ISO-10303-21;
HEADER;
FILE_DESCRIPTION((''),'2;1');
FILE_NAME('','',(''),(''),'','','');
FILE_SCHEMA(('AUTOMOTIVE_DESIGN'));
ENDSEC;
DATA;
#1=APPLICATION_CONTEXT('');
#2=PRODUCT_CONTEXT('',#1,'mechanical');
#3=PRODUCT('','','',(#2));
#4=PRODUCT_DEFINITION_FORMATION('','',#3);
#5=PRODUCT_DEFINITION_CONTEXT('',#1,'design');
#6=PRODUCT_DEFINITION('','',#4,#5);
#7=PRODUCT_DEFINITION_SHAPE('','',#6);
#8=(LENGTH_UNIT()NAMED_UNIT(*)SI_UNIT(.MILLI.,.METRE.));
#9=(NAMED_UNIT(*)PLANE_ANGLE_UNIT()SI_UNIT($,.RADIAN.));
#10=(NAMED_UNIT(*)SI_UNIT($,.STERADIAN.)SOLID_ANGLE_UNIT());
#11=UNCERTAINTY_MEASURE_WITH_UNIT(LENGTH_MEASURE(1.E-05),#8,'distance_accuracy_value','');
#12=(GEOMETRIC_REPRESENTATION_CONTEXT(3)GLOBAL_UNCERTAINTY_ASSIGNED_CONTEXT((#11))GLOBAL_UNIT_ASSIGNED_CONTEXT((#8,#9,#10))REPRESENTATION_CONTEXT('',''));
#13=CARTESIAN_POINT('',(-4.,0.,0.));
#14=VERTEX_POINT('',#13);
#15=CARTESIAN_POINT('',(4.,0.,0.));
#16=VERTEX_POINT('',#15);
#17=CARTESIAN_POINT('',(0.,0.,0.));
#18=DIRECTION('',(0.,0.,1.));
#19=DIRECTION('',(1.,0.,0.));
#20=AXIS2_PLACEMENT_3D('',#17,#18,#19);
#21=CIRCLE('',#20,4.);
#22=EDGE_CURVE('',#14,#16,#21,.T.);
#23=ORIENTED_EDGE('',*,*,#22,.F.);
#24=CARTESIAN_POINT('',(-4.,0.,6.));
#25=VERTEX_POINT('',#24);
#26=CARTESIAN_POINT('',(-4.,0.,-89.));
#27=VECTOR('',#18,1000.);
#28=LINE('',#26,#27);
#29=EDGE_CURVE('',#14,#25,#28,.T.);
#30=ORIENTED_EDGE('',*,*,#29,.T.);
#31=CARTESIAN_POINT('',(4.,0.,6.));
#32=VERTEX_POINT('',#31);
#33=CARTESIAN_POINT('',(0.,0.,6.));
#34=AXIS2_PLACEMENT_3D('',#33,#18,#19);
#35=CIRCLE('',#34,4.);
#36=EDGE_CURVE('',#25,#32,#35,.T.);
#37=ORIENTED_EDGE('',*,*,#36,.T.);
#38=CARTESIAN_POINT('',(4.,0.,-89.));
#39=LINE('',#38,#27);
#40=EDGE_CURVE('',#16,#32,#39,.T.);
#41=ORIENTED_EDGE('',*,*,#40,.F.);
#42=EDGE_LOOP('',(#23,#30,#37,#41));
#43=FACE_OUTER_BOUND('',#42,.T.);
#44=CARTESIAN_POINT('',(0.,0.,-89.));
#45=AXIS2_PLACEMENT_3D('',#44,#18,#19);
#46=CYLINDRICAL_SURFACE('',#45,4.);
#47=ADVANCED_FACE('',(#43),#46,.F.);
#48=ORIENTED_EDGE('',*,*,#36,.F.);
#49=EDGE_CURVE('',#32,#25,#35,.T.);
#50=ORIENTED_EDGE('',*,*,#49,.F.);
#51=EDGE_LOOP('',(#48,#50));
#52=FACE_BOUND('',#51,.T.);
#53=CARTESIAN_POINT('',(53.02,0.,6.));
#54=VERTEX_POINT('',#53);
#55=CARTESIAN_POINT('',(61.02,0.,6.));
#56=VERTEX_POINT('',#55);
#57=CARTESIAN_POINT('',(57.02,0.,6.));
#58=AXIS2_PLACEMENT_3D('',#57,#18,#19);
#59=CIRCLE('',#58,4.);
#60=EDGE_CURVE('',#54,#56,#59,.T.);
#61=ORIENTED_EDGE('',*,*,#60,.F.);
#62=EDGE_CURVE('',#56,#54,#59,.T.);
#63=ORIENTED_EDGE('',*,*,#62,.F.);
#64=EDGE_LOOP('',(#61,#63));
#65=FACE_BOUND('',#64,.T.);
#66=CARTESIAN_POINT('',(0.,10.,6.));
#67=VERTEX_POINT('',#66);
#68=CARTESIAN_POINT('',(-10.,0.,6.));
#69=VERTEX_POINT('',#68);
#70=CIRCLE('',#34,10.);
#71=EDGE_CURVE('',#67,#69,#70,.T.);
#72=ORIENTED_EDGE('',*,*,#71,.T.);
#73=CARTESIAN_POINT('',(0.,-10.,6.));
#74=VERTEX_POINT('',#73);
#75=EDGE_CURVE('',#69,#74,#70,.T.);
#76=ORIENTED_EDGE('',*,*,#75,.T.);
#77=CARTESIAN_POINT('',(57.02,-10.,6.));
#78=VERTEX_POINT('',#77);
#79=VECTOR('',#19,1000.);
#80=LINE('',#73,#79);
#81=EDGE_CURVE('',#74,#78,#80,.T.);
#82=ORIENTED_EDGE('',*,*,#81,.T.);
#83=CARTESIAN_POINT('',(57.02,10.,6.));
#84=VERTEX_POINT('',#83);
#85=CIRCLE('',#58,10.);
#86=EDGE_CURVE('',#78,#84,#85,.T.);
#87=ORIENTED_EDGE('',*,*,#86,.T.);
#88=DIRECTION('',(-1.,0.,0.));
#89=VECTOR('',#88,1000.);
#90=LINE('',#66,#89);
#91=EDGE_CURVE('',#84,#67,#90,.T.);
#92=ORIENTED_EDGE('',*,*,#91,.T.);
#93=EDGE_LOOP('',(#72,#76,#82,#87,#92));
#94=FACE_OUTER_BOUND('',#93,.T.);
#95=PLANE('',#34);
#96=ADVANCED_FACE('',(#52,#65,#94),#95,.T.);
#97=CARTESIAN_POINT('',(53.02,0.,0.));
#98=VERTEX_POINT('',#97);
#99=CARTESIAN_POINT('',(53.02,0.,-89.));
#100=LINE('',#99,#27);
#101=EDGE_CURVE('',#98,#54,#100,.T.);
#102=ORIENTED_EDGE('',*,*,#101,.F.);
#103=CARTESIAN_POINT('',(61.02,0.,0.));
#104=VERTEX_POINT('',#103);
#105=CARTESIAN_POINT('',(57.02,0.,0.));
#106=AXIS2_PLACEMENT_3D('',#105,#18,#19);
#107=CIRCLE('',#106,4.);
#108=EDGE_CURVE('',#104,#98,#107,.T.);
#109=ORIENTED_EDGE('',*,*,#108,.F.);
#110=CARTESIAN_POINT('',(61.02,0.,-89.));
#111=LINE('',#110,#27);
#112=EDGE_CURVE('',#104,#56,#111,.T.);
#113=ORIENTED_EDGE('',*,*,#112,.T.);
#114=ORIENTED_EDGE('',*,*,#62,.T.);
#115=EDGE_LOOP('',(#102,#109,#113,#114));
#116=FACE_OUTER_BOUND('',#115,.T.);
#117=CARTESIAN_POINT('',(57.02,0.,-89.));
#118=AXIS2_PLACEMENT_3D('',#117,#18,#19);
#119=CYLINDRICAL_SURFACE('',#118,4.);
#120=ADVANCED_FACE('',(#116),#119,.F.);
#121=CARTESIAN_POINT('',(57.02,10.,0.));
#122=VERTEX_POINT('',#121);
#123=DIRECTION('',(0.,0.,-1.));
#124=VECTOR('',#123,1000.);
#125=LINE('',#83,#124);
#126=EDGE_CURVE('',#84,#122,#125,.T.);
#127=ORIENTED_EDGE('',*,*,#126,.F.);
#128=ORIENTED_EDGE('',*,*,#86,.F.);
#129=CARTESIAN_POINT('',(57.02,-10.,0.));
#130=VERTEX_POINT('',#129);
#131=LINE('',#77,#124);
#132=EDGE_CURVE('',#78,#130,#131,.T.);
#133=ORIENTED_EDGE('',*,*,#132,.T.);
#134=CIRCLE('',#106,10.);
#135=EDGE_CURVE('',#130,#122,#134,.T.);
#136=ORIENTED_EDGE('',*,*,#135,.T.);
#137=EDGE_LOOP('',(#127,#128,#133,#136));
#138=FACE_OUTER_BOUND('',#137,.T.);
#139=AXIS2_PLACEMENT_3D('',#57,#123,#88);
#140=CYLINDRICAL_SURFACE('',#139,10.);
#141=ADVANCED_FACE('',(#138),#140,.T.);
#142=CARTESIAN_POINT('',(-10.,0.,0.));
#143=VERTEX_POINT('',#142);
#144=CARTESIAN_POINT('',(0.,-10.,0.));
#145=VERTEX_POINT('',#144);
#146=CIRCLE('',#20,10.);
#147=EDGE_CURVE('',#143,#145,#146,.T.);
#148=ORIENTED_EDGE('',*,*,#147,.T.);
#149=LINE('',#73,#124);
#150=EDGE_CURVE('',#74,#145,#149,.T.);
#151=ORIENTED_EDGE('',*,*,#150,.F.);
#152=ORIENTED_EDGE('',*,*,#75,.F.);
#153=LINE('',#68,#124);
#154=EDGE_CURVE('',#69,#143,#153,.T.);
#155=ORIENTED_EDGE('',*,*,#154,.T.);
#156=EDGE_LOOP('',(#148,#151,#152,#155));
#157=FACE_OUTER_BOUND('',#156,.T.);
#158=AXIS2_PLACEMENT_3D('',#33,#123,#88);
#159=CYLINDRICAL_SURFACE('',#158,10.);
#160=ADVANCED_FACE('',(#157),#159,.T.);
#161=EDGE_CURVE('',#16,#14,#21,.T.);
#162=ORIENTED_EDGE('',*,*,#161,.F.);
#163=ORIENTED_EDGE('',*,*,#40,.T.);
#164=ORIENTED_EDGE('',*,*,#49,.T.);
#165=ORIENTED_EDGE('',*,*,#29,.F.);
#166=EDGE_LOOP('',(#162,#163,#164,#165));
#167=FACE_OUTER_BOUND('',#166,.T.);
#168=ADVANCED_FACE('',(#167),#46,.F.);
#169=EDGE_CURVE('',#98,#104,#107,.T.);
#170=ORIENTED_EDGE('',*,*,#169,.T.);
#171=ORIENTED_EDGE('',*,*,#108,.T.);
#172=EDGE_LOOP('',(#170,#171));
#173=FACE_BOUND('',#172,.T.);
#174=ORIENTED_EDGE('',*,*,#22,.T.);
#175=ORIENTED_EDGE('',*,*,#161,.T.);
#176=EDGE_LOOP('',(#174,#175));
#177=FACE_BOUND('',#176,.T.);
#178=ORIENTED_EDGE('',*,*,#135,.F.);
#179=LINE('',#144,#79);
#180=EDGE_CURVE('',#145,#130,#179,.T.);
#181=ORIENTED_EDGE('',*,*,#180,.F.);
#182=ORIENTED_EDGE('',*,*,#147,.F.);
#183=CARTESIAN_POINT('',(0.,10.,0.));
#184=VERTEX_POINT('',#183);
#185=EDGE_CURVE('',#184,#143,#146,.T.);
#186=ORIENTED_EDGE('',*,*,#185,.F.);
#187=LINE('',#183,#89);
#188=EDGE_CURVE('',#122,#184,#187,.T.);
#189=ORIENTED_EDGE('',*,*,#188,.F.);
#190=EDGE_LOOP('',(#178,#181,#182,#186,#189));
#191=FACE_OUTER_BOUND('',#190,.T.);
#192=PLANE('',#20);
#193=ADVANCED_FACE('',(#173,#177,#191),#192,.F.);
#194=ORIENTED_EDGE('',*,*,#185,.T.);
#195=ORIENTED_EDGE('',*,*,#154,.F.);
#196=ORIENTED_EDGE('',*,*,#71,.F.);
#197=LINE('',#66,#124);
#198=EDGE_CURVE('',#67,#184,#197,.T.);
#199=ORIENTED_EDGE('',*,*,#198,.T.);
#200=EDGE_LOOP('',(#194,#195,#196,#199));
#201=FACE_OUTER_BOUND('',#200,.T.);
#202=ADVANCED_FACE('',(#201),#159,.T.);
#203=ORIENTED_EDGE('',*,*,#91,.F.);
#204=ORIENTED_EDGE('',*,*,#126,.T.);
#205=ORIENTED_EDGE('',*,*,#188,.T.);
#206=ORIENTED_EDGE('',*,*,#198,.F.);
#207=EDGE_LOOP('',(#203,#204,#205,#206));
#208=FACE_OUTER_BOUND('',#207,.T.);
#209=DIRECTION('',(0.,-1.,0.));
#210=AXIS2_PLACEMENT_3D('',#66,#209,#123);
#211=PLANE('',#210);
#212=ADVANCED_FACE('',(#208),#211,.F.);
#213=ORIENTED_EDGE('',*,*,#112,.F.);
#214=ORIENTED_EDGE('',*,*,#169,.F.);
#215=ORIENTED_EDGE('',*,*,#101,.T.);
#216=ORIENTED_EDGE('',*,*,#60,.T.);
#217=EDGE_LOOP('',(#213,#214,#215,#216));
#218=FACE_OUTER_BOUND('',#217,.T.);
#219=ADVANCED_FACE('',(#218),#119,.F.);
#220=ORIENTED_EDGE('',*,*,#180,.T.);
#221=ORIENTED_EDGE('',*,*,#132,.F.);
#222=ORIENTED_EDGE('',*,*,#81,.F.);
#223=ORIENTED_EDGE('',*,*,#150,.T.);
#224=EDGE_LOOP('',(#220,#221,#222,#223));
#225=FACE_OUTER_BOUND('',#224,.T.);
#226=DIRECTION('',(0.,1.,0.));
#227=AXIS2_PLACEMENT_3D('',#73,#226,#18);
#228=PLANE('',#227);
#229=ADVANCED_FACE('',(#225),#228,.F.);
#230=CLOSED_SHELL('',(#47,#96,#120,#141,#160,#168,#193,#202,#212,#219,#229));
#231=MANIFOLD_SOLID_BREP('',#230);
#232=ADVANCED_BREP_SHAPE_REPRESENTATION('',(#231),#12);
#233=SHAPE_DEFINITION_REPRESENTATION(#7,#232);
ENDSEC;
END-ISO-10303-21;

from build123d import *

# Parameters (mm, degrees)
BOSS_EXTRUDE1_DEPTH = 6
SKETCH2_R           = 4
CUT_EXTRUDE1_DEPTH  = 95


with BuildPart() as part:
    # Sketch1 → Boss-Extrude1 (new body)
    with BuildSketch(Plane.XY):
        with BuildLine():
            Line((0, 10), (57.02, 10))
            ThreePointArc((57.02, 10), (67.02, 0), (57.02, -10))
            Line((57.02, -10), (0, -10))
            ThreePointArc((0, -10), (-10, 0), (0, 10))
        make_face()
    extrude(amount=BOSS_EXTRUDE1_DEPTH)

    # Sketch2 → Cut-Extrude1 (cut)
    with BuildSketch(Plane.XY.offset(6)):
        Circle(SKETCH2_R)
        with Locations((57.02, 0)):
            Circle(SKETCH2_R)
    extrude(amount=-CUT_EXTRUDE1_DEPTH, mode=Mode.SUBTRACT)


solid = part.part
